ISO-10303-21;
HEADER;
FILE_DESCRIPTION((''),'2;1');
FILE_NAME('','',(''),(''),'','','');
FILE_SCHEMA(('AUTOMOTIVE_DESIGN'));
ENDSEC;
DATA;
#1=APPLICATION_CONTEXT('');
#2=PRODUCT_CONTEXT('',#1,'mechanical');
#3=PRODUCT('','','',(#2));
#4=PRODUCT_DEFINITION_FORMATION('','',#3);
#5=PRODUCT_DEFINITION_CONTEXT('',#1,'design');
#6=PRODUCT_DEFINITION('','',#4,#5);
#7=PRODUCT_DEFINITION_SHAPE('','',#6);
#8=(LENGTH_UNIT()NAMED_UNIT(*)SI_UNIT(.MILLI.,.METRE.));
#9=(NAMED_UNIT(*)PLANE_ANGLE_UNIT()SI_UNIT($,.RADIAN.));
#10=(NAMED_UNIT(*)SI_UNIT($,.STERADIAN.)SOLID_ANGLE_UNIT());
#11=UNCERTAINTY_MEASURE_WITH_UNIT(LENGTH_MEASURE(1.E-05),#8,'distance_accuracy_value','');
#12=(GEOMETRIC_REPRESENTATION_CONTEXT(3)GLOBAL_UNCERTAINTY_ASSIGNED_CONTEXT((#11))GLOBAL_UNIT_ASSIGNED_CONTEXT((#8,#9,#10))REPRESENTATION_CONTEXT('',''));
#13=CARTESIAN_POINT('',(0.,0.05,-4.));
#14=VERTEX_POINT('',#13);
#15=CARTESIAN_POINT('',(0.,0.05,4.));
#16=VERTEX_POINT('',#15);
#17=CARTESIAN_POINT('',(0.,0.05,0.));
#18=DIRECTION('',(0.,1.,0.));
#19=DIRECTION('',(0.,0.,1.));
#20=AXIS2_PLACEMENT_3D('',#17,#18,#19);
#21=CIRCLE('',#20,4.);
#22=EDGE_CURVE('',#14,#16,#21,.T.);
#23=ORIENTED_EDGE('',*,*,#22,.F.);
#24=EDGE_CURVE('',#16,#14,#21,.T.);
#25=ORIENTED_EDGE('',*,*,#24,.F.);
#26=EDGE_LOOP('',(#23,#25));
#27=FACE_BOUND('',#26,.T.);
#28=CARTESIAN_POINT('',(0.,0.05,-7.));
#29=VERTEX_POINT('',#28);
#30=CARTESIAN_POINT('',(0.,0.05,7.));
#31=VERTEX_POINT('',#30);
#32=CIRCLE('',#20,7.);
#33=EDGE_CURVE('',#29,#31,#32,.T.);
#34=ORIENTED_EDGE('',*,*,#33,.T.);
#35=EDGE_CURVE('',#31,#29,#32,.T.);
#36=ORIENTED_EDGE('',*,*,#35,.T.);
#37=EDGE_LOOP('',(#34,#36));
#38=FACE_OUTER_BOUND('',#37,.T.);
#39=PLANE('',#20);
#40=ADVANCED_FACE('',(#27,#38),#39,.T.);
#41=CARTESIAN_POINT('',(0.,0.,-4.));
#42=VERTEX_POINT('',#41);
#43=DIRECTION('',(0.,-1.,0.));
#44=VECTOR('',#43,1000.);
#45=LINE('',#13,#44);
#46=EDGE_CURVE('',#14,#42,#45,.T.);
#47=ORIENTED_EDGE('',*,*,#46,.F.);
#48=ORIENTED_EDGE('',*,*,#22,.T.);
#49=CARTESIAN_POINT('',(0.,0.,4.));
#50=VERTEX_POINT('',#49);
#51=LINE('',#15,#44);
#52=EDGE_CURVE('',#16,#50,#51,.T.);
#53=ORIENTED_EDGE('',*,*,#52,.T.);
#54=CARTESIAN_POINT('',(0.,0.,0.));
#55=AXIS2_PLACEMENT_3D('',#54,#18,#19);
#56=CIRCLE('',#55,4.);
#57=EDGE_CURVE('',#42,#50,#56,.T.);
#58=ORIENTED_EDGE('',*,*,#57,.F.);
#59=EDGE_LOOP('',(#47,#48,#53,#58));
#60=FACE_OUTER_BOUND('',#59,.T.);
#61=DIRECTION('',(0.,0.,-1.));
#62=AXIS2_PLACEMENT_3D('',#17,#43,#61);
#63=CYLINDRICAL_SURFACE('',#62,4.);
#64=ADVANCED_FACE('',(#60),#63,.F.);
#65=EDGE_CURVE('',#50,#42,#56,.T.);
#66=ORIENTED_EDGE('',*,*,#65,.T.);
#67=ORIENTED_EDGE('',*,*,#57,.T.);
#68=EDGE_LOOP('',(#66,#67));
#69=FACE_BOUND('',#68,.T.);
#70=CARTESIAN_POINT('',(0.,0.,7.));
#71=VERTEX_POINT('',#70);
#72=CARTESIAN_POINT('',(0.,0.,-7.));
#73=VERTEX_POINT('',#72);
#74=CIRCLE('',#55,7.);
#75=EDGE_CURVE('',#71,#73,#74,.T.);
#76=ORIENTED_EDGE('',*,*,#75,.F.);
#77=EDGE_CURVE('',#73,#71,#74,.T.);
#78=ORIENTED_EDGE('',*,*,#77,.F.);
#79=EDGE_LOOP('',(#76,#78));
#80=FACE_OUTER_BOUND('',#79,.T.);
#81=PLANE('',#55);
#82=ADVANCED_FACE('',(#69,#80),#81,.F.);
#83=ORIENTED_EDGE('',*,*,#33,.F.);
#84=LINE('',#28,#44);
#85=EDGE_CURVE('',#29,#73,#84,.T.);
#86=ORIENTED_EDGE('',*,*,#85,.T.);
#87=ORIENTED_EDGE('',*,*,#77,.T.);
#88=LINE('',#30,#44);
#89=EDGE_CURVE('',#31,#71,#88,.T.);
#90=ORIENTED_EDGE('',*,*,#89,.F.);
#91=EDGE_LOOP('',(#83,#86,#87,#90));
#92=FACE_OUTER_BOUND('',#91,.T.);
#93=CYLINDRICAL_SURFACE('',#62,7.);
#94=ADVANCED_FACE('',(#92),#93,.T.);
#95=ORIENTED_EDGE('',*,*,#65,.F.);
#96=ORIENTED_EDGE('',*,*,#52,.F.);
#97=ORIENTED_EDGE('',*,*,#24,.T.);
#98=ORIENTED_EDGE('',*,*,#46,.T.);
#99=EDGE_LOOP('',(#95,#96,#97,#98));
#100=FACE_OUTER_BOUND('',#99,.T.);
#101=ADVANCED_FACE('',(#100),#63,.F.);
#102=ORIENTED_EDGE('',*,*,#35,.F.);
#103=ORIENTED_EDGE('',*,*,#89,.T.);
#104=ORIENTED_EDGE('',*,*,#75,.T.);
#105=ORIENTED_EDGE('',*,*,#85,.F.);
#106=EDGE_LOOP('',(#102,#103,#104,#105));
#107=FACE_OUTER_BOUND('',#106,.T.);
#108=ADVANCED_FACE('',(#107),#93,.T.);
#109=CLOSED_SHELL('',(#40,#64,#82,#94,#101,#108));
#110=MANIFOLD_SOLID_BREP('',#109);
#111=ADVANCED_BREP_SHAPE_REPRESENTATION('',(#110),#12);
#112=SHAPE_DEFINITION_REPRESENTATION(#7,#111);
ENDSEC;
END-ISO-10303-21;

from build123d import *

# Parameters (mm, degrees)
SKETCH1_R           = 7
SKETCH1_R_2         = 4
BOSS_EXTRUDE1_DEPTH = 0.05


with BuildPart() as part:
    # Sketch1 → Boss-Extrude1 (new body)
    with BuildSketch(Plane(origin=(0, 0, 0), x_dir=(1, 0, 0), z_dir=(0, 1, 0))):
        with Locations(Location((0, 0, 0), (0, 0, 270))):
            Circle(SKETCH1_R)
        with Locations(Location((0, 0, 0), (0, 0, 270))):
            Circle(SKETCH1_R_2, mode=Mode.SUBTRACT)
    extrude(amount=BOSS_EXTRUDE1_DEPTH)


solid = part.part
